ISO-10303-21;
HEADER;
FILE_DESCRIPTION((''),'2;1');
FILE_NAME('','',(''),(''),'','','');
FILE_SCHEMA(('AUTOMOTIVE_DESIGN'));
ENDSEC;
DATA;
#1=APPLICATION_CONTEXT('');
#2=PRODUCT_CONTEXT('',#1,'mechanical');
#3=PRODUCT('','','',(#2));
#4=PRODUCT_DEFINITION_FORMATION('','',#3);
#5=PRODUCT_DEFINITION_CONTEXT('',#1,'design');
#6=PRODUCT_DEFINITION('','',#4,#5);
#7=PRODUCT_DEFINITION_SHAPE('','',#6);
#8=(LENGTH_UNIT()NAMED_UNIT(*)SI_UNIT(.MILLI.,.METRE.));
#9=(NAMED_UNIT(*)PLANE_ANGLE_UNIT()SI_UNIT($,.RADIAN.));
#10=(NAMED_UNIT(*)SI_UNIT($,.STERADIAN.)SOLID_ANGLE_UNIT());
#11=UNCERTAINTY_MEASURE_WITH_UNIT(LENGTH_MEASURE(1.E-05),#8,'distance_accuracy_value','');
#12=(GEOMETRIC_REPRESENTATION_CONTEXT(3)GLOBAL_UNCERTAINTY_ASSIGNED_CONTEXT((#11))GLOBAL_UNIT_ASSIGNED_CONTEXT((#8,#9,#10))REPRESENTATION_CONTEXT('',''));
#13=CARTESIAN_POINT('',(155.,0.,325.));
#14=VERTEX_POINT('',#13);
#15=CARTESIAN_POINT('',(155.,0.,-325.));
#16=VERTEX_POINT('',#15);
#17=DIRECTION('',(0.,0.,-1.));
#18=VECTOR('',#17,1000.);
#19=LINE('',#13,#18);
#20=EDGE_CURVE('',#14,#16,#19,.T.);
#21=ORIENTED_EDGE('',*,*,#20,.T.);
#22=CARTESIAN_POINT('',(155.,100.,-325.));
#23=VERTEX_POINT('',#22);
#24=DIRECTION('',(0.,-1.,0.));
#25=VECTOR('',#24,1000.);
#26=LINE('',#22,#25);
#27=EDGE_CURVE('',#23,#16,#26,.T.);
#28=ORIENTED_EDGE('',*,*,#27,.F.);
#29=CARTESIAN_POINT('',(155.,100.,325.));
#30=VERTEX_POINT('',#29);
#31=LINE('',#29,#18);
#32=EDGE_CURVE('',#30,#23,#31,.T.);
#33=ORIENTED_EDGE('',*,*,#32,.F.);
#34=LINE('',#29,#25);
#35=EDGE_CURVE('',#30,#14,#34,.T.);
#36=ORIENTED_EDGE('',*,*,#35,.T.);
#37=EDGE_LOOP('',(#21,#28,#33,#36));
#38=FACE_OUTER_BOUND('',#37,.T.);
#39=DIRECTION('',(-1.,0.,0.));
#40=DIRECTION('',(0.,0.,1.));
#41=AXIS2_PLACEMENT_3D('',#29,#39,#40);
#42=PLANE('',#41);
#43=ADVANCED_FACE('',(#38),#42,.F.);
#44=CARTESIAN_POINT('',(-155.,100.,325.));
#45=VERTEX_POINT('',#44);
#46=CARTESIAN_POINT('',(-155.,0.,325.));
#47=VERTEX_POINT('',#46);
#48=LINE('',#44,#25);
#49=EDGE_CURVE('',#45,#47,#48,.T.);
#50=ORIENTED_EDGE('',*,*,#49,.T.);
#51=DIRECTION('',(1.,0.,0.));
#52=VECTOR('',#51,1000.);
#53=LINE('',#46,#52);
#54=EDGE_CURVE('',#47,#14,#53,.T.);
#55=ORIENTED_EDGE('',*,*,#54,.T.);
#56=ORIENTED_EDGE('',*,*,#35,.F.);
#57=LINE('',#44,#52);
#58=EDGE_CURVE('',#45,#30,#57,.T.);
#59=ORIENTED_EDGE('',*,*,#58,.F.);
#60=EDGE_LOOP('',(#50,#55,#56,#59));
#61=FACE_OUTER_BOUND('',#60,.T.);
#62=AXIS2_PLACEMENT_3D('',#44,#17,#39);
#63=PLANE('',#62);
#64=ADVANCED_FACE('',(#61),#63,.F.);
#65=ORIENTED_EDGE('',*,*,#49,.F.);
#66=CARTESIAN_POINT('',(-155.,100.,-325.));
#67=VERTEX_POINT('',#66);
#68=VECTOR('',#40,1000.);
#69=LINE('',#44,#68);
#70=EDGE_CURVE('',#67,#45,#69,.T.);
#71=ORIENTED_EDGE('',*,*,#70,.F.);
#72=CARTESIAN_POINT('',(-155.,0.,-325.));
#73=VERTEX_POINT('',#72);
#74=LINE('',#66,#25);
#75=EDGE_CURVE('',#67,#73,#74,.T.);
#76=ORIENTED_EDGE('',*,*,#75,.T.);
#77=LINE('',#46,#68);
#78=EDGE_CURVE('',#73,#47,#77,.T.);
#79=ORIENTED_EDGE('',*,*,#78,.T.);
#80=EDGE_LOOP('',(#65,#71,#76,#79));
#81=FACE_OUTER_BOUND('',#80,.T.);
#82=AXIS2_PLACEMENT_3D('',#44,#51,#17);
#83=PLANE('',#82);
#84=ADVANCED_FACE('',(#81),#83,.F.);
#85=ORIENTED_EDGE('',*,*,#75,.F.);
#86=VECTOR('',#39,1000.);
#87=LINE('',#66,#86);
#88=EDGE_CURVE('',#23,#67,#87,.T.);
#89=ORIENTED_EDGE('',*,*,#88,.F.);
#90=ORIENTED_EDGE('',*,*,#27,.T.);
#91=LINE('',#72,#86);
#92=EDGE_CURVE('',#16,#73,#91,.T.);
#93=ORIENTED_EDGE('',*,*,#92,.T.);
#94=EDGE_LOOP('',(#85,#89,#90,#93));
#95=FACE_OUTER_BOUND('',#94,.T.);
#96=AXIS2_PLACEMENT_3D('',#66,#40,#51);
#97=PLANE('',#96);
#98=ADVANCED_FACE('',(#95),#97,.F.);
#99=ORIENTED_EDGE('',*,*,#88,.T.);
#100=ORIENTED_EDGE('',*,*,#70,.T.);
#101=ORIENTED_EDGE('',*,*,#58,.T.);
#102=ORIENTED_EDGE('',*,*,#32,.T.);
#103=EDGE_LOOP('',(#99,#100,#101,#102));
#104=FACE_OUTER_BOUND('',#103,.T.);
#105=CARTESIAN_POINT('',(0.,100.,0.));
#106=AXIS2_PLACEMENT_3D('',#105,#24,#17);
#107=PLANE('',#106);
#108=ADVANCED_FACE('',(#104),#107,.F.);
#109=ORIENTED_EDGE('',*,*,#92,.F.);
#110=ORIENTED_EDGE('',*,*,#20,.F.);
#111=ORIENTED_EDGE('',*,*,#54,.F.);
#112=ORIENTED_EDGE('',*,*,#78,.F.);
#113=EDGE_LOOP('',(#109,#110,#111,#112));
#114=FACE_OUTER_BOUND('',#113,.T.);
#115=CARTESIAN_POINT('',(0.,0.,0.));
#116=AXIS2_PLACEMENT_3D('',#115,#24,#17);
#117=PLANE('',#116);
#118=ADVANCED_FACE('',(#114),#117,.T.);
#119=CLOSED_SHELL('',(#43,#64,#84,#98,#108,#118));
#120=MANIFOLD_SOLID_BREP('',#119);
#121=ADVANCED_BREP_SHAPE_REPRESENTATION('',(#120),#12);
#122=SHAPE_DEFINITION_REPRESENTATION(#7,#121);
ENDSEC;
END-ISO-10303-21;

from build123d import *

# Parameters (mm, degrees)
SKETCH_1_W      = 310
SKETCH_1_H      = 650
EXTRUDE_1_DEPTH = 100


with BuildPart() as part:
    # 草图1 → 凸台-拉伸1 (new body)
    with BuildSketch(Plane(origin=(0, 0, 0), x_dir=(1, 0, 0), z_dir=(0, 1, 0))):
        Rectangle(SKETCH_1_W, SKETCH_1_H)
    extrude(amount=EXTRUDE_1_DEPTH)


solid = part.part
